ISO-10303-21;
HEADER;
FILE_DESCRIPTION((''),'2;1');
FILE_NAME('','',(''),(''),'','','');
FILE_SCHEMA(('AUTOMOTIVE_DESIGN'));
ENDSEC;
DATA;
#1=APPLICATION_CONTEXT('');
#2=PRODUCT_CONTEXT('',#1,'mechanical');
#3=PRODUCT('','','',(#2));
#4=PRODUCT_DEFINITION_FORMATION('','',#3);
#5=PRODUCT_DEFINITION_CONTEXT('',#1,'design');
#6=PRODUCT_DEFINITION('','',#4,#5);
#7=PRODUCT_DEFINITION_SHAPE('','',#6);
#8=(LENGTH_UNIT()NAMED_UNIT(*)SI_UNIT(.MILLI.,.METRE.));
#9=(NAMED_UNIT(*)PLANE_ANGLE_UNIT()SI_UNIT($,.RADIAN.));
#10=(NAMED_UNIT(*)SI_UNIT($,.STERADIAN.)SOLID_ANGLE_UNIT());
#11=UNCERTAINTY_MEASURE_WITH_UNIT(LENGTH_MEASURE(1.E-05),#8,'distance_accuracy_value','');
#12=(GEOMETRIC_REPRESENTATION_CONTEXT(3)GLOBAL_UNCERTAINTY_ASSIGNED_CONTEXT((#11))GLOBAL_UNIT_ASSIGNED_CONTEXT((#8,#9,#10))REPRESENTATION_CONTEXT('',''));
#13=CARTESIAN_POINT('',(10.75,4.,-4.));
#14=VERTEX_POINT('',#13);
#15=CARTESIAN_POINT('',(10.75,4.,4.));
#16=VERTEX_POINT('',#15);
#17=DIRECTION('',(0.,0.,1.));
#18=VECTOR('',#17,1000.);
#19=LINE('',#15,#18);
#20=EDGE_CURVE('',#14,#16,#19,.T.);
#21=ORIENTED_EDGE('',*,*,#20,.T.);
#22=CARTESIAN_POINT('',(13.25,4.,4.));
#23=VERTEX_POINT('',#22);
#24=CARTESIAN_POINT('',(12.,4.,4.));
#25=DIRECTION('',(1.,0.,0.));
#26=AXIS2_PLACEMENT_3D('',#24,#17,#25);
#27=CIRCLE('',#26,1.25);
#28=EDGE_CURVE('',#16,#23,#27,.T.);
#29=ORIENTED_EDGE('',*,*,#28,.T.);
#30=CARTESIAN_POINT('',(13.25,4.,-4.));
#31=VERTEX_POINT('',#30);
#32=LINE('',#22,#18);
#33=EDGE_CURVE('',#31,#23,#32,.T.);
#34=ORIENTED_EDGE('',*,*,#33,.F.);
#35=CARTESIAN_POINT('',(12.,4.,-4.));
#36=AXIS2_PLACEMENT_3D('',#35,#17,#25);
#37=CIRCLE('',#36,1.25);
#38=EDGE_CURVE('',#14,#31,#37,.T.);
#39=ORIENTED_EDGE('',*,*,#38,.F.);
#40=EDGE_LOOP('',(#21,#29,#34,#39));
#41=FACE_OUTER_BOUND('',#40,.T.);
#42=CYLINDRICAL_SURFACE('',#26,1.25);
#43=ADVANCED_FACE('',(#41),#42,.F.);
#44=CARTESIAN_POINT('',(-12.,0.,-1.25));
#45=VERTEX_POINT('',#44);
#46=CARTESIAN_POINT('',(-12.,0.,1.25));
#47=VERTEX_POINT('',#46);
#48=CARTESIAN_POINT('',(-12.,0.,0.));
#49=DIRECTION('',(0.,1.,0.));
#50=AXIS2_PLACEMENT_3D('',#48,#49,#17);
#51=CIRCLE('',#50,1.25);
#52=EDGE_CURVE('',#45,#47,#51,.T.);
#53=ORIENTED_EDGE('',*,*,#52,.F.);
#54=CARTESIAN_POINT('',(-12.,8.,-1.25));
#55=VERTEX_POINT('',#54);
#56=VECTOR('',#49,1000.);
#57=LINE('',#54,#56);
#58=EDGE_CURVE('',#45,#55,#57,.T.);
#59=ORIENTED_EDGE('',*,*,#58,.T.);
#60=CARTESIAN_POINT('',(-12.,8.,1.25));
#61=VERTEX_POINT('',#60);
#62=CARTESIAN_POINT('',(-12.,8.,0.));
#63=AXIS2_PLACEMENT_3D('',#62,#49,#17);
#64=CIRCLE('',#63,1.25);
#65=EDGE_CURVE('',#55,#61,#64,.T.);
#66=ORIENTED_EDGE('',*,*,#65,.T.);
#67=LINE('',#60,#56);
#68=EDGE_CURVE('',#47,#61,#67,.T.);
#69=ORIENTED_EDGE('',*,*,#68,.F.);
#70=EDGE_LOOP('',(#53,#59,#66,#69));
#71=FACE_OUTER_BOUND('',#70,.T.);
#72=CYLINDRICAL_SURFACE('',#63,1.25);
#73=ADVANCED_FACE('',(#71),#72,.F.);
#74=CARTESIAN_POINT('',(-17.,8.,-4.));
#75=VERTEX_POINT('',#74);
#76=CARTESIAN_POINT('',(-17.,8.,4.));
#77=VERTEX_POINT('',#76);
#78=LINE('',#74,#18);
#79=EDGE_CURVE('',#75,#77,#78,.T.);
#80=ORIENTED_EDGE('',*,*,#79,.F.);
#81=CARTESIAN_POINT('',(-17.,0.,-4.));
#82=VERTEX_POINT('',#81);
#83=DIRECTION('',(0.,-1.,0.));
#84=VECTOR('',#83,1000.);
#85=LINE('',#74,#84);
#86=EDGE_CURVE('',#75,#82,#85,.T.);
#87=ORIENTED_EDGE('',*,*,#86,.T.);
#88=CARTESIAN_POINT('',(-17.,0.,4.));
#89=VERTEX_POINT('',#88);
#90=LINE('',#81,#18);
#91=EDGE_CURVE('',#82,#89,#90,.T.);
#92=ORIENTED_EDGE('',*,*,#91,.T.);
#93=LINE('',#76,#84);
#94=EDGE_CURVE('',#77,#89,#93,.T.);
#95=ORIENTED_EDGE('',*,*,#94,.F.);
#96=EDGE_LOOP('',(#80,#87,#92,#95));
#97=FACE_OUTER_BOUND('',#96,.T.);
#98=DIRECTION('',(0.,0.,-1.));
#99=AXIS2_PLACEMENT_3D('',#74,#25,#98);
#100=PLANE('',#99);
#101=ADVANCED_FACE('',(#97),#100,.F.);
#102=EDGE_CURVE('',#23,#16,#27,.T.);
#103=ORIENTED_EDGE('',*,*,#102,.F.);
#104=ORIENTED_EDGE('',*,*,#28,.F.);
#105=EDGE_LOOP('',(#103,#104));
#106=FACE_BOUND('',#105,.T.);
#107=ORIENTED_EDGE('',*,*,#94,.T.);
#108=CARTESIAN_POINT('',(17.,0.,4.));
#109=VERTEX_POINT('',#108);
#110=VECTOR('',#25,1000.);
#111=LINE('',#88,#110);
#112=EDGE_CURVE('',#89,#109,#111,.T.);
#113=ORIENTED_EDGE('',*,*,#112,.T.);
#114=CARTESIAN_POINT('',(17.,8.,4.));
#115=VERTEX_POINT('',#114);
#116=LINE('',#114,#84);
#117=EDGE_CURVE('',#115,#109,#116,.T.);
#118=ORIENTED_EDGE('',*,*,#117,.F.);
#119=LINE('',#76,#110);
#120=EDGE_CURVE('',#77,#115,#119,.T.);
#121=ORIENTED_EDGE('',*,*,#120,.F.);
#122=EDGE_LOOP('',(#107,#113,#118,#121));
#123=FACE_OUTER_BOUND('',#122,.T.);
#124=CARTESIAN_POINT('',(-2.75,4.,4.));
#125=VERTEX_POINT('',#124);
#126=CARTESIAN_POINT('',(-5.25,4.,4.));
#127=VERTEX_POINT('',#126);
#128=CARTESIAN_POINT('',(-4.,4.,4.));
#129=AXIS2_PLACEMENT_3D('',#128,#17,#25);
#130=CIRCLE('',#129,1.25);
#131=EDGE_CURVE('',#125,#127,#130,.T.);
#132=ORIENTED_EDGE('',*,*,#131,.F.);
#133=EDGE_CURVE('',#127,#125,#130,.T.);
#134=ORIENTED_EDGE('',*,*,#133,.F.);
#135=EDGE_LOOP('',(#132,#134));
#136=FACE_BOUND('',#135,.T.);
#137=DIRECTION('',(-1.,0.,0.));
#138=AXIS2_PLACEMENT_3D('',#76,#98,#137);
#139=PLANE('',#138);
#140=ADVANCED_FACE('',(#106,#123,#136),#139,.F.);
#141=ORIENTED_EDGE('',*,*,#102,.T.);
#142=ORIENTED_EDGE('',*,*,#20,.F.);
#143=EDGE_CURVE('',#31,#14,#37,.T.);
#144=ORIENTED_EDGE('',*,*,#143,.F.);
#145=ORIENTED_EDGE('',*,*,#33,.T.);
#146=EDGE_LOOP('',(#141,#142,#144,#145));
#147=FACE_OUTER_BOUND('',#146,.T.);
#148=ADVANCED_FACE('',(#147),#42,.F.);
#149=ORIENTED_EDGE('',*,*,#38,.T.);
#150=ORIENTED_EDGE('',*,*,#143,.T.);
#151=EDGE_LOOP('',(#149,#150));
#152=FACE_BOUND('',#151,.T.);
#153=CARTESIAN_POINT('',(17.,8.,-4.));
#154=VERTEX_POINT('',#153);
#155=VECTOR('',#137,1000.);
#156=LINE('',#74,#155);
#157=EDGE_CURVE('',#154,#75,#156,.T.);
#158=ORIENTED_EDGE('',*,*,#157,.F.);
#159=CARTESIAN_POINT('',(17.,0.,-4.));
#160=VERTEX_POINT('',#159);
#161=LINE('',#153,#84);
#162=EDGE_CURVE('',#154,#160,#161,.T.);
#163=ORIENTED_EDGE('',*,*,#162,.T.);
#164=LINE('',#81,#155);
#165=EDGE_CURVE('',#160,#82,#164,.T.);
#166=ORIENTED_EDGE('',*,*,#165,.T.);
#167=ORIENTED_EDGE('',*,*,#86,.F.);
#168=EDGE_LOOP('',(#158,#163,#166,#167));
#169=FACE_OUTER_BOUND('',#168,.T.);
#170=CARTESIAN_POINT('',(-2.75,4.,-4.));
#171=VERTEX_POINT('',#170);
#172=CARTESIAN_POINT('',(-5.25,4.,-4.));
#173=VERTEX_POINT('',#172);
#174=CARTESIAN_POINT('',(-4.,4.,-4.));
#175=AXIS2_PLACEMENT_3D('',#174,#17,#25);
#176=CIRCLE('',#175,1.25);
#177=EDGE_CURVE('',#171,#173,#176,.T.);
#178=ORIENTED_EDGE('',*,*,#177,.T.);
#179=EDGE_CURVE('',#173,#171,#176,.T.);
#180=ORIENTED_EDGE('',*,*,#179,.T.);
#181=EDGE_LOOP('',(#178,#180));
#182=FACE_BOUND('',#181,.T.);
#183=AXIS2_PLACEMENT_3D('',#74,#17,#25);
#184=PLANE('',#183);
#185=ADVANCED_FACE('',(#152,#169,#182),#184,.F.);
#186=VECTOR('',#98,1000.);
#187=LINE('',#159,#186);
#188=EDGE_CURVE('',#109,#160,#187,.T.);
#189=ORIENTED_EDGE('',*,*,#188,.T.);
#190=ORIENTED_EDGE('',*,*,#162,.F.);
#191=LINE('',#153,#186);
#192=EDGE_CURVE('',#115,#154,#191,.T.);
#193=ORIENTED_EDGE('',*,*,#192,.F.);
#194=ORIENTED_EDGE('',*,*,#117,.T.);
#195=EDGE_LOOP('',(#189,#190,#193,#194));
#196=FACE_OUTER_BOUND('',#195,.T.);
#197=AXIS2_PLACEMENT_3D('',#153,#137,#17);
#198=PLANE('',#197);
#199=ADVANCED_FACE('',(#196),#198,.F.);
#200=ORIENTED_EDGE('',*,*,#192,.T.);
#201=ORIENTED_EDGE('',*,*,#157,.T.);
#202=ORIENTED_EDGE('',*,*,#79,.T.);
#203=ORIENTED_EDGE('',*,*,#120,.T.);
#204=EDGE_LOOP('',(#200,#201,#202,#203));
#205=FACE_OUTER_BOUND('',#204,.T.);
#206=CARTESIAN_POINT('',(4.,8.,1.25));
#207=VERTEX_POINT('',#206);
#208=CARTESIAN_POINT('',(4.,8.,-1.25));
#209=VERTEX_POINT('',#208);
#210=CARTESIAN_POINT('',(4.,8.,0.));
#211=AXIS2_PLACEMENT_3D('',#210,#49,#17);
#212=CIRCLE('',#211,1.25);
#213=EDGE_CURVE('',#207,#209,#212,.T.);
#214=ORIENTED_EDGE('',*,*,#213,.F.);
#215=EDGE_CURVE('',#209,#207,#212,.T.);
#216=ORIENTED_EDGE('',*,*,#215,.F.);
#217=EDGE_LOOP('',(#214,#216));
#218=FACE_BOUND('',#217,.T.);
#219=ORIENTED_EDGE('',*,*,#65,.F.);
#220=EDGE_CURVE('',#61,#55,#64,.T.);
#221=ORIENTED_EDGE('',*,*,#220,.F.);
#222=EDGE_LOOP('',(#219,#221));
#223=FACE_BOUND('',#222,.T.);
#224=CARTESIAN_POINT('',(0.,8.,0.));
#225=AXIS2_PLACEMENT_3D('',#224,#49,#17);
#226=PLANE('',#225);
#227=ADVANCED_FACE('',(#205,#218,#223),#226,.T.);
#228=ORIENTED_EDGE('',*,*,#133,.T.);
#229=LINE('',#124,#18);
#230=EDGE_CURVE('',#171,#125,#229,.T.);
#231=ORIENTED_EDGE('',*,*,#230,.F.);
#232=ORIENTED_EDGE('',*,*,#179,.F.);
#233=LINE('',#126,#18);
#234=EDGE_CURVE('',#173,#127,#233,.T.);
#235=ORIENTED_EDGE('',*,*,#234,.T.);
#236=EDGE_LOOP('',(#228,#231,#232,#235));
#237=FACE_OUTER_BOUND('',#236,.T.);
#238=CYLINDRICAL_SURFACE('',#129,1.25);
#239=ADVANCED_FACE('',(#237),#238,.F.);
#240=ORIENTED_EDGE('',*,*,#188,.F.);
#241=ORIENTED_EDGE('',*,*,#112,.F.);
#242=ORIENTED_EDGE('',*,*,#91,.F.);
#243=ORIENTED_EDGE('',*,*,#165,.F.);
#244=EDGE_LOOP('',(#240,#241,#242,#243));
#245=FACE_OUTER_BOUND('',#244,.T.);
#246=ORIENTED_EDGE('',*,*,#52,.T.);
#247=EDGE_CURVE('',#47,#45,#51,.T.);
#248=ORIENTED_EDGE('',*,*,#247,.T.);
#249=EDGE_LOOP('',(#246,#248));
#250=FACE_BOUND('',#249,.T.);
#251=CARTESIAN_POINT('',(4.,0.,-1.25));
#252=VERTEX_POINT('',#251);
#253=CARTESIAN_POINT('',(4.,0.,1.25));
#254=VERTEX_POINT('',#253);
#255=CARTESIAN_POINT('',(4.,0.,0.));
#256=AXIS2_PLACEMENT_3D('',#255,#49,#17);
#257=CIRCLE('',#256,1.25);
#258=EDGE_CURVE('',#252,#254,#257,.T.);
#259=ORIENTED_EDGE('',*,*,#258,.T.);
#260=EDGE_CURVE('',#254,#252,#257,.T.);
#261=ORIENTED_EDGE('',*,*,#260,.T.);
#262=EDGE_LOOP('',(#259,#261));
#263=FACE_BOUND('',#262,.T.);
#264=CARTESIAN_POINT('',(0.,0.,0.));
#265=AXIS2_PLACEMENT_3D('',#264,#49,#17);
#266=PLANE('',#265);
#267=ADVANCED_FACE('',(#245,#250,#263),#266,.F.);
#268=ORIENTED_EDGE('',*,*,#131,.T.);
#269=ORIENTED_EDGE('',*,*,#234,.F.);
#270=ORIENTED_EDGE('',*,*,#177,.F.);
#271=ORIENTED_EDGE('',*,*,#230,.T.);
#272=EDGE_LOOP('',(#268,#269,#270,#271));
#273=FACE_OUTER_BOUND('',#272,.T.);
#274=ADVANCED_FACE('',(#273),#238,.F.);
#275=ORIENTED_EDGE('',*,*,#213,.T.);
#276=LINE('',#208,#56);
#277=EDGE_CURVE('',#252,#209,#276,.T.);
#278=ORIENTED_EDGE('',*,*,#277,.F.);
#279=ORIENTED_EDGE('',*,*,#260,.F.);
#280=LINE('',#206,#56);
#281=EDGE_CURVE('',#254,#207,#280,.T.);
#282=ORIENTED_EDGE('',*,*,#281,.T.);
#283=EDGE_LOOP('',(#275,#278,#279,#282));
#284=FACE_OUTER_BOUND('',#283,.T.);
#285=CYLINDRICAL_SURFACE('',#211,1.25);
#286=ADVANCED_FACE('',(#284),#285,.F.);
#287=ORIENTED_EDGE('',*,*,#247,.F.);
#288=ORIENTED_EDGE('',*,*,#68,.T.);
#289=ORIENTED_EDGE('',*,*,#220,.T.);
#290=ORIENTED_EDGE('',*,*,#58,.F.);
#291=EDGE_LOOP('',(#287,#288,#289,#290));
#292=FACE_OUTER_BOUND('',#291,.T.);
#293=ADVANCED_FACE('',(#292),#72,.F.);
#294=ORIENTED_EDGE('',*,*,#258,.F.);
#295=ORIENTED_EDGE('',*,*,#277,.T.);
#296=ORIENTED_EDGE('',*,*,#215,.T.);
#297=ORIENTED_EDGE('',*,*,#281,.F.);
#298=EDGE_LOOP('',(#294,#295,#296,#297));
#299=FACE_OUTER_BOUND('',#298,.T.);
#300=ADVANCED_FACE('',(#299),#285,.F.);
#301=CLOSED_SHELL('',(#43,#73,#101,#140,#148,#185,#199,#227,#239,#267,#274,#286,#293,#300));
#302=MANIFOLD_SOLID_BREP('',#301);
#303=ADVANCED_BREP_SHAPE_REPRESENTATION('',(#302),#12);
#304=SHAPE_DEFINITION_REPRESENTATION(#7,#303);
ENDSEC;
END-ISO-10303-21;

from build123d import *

# Parameters (mm, degrees)
SKETCH_1_W         = 34
SKETCH_1_H         = 8
EXTRUDE_1_DEPTH    = 8
HOLE_WIZARD_M3_1_D = 2.5
HOLE_WIZARD_M3_2_D = 2.5


with BuildPart() as part:
    # 草图1 → 凸台-拉伸1 (new body)
    with BuildSketch(Plane(origin=(0, 0, 0), x_dir=(1, 0, 0), z_dir=(0, 1, 0))):
        Rectangle(SKETCH_1_W, SKETCH_1_H)
    extrude(amount=EXTRUDE_1_DEPTH)

    # M3 螺纹孔1 (through all)
    with Locations(Plane(origin=(0, 8, 0), x_dir=(1, 0, 0), z_dir=(0, 1, 0))):
        with Locations((4, 0), (-12, 0)):
            Hole(HOLE_WIZARD_M3_1_D / 2)

    # M3 螺纹孔2 (through all)
    with Locations(Plane.XY.offset(4)):
        with Locations((12, 4), (-4, 4)):
            Hole(HOLE_WIZARD_M3_2_D / 2)


solid = part.part
